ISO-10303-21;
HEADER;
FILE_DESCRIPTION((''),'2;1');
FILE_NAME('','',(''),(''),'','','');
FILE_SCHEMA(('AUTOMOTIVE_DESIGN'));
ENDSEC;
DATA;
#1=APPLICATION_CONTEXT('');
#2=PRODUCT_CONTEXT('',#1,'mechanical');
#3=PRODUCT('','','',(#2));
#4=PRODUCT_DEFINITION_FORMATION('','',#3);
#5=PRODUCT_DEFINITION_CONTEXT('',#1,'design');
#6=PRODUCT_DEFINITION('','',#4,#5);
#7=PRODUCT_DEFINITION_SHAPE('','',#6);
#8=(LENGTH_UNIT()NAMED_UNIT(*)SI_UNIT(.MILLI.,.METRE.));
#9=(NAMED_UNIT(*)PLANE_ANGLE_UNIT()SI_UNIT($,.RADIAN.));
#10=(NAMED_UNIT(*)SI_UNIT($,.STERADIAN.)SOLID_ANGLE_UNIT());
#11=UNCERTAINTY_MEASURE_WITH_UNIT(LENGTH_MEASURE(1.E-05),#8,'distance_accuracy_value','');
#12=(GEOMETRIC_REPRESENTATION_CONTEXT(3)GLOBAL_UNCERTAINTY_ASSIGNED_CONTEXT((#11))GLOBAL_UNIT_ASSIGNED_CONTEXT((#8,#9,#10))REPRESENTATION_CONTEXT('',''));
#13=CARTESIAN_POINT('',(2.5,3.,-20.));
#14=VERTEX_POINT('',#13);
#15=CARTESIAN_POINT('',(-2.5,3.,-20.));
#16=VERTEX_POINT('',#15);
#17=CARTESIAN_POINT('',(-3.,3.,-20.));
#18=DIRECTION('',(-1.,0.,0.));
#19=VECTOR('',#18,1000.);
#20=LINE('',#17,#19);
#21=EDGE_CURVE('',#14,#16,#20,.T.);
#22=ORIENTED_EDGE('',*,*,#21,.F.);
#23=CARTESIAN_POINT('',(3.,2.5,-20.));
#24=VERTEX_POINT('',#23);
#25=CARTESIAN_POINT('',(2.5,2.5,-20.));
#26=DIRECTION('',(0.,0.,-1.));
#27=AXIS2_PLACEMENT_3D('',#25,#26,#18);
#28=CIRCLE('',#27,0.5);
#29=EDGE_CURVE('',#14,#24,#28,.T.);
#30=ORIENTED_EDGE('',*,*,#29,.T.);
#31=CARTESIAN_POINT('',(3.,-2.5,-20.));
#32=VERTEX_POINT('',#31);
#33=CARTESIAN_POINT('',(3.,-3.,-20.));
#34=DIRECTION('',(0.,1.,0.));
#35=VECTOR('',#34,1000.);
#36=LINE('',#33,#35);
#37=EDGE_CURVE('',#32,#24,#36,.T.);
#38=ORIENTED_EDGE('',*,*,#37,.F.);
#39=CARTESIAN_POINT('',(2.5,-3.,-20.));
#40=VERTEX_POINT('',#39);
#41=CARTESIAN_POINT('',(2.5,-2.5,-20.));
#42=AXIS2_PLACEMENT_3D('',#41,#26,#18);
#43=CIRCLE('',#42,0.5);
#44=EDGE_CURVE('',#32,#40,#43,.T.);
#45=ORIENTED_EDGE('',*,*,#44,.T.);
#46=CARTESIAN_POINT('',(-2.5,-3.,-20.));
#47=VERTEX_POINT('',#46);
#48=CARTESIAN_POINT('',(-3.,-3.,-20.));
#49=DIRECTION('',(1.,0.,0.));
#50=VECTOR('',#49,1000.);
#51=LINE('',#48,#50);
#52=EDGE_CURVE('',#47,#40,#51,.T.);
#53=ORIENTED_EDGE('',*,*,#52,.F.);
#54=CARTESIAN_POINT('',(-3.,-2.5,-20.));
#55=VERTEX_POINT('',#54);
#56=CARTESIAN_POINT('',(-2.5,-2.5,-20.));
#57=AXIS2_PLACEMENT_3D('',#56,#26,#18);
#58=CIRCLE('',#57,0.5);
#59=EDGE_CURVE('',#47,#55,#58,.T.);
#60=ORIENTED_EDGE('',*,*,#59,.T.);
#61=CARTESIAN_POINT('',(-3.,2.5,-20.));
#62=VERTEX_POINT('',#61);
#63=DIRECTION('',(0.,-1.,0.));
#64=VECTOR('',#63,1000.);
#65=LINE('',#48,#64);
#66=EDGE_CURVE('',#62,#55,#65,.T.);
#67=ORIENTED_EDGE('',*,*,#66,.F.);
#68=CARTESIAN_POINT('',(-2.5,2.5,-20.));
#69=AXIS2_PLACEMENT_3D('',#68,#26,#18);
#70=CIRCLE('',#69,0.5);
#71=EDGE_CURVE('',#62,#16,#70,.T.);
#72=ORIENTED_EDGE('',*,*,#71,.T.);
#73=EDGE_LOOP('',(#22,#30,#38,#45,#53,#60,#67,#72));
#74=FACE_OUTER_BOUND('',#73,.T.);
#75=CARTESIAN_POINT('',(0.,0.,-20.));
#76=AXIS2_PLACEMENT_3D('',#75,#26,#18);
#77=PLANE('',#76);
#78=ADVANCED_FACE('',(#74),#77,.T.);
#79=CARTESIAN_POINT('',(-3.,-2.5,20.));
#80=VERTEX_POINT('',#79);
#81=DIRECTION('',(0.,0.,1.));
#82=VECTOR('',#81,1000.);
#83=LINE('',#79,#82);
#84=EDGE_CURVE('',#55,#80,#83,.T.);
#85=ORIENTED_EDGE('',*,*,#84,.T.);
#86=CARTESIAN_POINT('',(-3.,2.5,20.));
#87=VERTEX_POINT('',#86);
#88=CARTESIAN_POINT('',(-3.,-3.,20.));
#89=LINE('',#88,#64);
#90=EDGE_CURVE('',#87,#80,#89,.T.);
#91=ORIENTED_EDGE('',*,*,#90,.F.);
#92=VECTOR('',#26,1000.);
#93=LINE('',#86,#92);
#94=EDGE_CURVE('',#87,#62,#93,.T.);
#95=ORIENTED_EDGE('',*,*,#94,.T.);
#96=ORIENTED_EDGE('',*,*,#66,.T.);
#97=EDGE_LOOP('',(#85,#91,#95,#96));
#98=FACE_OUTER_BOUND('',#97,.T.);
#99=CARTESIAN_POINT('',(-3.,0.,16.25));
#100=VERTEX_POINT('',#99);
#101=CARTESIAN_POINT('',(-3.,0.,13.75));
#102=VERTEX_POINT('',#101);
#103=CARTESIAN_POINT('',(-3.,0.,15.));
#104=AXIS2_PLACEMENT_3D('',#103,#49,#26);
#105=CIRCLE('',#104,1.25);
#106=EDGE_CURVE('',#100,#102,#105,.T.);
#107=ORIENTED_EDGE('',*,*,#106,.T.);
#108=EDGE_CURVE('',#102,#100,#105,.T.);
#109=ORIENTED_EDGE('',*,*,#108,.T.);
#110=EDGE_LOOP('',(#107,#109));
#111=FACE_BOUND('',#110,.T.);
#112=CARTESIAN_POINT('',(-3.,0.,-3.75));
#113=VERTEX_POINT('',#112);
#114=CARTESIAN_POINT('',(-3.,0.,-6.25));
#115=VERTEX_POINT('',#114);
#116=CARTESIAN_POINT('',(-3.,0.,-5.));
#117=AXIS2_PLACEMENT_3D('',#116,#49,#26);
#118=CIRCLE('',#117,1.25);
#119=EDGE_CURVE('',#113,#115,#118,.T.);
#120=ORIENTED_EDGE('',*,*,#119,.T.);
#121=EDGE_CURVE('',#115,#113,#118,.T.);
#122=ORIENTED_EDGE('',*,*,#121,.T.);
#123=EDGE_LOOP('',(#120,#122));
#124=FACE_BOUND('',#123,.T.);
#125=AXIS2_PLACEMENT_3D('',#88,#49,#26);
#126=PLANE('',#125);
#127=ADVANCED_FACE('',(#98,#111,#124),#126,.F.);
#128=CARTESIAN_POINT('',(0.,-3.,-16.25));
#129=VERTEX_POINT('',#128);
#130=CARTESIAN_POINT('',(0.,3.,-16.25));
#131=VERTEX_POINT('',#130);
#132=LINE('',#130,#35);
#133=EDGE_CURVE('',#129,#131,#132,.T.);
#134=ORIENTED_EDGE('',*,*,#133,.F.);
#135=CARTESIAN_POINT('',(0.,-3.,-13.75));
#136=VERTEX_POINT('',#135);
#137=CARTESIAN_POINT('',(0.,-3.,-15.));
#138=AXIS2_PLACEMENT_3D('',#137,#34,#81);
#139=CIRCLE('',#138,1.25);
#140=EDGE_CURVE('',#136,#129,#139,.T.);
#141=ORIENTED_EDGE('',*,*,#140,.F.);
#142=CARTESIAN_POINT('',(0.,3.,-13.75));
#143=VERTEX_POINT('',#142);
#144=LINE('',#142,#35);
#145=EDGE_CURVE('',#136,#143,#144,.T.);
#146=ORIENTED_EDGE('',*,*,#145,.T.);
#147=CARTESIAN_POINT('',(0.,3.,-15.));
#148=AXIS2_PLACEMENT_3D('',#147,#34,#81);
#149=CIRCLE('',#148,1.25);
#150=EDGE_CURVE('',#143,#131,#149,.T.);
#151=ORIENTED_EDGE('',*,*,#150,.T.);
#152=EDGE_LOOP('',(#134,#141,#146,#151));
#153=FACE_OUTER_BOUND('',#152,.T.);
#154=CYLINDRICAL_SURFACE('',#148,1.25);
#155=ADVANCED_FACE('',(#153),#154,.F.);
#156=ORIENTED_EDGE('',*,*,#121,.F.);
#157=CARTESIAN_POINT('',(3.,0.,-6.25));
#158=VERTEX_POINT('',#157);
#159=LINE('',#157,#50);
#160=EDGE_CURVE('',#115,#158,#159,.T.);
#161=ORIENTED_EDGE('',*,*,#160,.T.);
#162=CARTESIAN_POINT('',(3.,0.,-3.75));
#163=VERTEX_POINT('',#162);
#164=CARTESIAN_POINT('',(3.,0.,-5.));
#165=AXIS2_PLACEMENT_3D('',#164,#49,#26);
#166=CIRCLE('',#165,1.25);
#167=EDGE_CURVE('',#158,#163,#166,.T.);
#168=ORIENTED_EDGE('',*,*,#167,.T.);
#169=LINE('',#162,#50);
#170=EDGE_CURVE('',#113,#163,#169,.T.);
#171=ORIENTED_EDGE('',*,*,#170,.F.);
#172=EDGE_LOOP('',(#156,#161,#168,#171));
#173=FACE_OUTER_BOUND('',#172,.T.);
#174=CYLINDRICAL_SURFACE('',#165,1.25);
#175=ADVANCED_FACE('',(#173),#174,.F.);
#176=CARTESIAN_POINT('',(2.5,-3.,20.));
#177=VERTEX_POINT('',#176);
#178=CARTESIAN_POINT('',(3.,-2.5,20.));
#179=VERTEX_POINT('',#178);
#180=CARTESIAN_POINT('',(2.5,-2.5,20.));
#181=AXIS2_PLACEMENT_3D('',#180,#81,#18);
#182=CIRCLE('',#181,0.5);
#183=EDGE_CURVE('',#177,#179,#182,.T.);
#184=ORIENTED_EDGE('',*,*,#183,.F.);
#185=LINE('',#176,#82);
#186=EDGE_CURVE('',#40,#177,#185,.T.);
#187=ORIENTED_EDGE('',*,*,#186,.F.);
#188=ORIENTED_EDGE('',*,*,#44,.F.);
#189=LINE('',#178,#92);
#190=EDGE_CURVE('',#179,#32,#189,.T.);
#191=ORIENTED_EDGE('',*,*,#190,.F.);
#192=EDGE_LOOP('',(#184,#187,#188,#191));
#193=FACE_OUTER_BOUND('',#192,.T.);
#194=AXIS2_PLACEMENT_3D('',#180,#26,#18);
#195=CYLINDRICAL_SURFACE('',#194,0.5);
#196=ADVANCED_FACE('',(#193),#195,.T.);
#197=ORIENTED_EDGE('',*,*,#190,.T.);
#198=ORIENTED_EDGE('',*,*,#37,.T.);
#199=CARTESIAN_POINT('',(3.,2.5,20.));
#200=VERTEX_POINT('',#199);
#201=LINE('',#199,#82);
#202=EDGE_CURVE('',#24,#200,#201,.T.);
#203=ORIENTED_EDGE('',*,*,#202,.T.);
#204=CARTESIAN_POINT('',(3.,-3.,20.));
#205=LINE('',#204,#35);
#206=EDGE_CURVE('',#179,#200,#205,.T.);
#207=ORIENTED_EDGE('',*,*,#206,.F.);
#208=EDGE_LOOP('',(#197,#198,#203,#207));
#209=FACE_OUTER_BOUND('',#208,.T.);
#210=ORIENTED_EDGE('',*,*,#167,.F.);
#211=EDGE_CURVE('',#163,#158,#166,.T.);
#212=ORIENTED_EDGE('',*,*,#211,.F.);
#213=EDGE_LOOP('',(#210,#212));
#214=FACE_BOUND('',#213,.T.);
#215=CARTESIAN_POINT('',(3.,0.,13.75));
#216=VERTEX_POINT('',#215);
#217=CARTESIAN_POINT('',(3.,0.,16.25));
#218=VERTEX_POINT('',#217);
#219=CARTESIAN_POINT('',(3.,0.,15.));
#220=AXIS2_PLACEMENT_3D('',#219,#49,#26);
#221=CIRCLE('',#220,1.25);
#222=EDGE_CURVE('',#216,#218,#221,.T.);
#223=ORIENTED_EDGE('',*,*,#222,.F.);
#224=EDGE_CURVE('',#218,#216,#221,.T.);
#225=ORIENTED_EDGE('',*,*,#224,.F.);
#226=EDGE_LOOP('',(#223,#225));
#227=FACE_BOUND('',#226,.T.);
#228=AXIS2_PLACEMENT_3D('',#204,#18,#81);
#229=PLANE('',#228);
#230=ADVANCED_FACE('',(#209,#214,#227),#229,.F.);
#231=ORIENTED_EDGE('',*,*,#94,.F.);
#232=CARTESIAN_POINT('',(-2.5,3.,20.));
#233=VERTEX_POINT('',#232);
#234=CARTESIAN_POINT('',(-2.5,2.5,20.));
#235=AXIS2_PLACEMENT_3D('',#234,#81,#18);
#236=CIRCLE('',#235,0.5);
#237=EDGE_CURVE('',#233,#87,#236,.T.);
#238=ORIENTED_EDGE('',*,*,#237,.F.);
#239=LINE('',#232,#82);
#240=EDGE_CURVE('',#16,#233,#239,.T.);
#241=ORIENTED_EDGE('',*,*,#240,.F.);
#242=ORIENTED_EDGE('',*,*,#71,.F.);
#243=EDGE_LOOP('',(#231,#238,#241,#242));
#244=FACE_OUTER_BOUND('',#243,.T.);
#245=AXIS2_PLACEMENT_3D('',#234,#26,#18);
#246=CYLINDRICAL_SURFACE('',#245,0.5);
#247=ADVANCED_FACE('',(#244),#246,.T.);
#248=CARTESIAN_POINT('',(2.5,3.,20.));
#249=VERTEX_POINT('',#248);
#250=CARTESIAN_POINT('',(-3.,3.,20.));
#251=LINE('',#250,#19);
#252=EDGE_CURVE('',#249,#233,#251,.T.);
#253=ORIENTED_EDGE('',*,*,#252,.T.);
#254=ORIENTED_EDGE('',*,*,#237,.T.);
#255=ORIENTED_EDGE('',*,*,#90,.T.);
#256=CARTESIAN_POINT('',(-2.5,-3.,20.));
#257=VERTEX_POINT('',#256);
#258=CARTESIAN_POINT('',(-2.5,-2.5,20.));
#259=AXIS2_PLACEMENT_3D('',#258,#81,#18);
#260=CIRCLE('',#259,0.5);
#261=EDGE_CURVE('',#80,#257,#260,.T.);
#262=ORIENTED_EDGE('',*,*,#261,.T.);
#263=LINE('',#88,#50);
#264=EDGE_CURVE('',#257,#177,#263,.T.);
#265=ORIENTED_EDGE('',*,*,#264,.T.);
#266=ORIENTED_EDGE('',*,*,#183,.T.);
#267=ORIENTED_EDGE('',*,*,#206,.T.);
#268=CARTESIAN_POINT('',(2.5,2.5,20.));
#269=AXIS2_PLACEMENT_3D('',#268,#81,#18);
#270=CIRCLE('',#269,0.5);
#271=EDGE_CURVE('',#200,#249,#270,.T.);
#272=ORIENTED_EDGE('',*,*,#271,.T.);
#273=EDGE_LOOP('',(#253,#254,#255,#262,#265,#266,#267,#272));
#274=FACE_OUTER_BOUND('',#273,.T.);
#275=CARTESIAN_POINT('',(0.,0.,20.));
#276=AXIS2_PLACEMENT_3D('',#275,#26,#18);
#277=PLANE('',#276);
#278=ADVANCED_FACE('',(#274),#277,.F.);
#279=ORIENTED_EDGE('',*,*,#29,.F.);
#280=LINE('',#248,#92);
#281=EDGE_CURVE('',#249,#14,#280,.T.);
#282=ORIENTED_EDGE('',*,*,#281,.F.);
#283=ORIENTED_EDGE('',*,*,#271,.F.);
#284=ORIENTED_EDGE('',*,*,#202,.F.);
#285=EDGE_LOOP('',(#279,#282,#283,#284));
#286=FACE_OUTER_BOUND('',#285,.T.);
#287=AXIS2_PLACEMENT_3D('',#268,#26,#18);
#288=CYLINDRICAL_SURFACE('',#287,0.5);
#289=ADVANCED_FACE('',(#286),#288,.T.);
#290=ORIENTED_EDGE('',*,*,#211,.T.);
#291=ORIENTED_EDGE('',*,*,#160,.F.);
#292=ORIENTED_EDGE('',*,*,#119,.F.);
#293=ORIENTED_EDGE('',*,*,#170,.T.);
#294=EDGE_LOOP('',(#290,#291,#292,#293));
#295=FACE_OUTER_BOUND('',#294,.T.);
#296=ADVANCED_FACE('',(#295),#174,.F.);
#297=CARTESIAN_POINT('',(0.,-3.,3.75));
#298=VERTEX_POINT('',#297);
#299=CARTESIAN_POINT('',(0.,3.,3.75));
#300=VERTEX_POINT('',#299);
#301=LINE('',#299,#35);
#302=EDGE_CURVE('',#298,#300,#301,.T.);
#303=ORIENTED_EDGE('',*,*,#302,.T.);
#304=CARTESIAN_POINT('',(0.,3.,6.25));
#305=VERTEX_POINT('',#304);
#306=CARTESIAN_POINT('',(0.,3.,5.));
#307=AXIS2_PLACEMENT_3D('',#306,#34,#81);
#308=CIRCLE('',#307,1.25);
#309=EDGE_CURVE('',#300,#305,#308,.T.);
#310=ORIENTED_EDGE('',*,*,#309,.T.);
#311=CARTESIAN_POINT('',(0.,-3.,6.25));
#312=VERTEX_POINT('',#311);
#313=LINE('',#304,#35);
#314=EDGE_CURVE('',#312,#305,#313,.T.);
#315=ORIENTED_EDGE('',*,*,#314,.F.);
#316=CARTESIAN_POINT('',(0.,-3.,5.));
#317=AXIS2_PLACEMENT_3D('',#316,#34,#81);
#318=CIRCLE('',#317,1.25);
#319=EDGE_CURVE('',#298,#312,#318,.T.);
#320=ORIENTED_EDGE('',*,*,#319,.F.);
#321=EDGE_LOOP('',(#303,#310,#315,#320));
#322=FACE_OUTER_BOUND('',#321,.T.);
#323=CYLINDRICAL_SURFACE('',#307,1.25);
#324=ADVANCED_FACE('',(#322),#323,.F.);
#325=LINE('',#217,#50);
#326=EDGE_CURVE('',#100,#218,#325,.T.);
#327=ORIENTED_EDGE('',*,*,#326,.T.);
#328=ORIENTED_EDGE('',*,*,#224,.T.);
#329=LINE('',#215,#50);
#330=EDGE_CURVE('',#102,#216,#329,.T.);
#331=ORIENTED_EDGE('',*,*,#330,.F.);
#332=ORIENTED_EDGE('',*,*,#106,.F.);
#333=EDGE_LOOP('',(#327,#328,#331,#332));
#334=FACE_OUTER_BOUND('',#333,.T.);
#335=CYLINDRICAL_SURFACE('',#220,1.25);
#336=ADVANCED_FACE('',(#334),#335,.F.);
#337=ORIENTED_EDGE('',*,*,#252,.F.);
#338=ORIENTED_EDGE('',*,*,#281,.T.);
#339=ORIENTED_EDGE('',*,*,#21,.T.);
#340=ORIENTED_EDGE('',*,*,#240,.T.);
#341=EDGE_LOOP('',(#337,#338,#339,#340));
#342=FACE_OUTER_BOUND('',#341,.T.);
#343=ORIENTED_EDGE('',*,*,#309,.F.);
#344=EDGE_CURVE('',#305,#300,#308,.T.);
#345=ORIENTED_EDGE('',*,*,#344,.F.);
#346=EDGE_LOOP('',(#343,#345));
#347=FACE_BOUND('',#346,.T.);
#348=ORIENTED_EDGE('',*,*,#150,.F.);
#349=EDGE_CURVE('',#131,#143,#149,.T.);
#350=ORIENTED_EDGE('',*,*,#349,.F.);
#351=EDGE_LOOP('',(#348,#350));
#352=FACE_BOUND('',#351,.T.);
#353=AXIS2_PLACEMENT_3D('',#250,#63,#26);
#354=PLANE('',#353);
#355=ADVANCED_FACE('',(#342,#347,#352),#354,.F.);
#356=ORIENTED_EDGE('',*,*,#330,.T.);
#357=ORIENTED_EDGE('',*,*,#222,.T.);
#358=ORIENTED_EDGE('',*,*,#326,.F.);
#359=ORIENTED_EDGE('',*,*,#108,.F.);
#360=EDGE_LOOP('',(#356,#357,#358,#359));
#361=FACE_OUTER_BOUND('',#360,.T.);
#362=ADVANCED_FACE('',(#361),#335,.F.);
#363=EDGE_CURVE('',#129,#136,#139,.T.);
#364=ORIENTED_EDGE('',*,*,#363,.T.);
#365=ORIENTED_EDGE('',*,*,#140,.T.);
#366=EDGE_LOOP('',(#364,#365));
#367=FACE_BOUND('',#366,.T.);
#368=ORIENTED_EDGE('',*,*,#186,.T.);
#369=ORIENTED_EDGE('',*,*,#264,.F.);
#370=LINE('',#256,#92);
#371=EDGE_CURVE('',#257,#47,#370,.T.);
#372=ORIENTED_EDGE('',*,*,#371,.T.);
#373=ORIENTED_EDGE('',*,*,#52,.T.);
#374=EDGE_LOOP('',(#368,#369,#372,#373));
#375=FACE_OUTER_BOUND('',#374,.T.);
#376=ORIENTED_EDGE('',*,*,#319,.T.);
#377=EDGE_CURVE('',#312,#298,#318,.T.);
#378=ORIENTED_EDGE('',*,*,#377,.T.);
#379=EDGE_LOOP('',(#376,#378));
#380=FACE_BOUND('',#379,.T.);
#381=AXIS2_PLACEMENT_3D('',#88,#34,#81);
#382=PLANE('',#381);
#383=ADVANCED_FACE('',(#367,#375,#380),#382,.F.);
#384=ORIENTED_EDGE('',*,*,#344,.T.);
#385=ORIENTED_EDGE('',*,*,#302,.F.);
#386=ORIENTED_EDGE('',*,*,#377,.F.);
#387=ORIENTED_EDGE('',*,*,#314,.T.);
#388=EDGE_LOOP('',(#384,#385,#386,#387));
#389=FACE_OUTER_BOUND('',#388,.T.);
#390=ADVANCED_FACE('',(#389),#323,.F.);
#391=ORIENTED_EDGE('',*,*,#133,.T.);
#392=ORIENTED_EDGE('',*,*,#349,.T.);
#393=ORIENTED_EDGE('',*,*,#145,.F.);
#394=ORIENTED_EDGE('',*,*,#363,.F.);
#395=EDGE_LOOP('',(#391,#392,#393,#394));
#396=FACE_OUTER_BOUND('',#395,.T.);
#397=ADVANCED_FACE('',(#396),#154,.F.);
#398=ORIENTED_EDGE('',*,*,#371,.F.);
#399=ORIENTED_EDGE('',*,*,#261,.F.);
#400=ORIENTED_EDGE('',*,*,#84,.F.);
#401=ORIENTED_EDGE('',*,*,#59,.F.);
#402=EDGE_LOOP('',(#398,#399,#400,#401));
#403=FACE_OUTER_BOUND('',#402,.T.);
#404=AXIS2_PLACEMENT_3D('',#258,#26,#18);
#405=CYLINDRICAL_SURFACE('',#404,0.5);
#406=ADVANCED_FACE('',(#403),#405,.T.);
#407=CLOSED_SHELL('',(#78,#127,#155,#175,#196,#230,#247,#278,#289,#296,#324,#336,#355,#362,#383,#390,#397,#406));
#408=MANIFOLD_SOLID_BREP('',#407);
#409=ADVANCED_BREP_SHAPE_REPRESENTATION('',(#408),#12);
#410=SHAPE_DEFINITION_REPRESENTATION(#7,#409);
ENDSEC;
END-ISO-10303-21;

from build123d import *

# Parameters (mm, degrees)
SKETCH_1_W         = 6
SKETCH_1_H         = 6
EXTRUDE_1_DEPTH    = 20
HOLE_WIZARD_M3_1_D = 2.5
HOLE_WIZARD_M3_2_D = 2.5
FILLET_1_R         = 0.5


with BuildPart() as part:
    # 草图1 → 凸台-拉伸1 (new, symmetric)
    with BuildSketch(Plane.XY):
        Rectangle(SKETCH_1_W, SKETCH_1_H)
    extrude(amount=EXTRUDE_1_DEPTH, both=True)

    # M3 螺纹孔1 (through all)
    with Locations(Plane(origin=(0, 3, 0), x_dir=(1, 0, 0), z_dir=(0, 1, 0))):
        with Locations((0, 15), (0, -5)):
            Hole(HOLE_WIZARD_M3_1_D / 2)

    # M3 螺纹孔2 (through all)
    with Locations(Plane(origin=(3, 0, 0), x_dir=(0, 0, -1), z_dir=(1, 0, 0))):
        with Locations((-15, 0), (5, 0)):
            Hole(HOLE_WIZARD_M3_2_D / 2)

    # 圆角1
    fillet_1_edges = [part.edges().sort_by_distance(p)[0] for p in [
        (3, -3, 0),
        (-3, -3, 0),
        (-3, 3, 0),
        (3, 3, 0),
    ]]
    fillet(fillet_1_edges, radius=FILLET_1_R)


solid = part.part
